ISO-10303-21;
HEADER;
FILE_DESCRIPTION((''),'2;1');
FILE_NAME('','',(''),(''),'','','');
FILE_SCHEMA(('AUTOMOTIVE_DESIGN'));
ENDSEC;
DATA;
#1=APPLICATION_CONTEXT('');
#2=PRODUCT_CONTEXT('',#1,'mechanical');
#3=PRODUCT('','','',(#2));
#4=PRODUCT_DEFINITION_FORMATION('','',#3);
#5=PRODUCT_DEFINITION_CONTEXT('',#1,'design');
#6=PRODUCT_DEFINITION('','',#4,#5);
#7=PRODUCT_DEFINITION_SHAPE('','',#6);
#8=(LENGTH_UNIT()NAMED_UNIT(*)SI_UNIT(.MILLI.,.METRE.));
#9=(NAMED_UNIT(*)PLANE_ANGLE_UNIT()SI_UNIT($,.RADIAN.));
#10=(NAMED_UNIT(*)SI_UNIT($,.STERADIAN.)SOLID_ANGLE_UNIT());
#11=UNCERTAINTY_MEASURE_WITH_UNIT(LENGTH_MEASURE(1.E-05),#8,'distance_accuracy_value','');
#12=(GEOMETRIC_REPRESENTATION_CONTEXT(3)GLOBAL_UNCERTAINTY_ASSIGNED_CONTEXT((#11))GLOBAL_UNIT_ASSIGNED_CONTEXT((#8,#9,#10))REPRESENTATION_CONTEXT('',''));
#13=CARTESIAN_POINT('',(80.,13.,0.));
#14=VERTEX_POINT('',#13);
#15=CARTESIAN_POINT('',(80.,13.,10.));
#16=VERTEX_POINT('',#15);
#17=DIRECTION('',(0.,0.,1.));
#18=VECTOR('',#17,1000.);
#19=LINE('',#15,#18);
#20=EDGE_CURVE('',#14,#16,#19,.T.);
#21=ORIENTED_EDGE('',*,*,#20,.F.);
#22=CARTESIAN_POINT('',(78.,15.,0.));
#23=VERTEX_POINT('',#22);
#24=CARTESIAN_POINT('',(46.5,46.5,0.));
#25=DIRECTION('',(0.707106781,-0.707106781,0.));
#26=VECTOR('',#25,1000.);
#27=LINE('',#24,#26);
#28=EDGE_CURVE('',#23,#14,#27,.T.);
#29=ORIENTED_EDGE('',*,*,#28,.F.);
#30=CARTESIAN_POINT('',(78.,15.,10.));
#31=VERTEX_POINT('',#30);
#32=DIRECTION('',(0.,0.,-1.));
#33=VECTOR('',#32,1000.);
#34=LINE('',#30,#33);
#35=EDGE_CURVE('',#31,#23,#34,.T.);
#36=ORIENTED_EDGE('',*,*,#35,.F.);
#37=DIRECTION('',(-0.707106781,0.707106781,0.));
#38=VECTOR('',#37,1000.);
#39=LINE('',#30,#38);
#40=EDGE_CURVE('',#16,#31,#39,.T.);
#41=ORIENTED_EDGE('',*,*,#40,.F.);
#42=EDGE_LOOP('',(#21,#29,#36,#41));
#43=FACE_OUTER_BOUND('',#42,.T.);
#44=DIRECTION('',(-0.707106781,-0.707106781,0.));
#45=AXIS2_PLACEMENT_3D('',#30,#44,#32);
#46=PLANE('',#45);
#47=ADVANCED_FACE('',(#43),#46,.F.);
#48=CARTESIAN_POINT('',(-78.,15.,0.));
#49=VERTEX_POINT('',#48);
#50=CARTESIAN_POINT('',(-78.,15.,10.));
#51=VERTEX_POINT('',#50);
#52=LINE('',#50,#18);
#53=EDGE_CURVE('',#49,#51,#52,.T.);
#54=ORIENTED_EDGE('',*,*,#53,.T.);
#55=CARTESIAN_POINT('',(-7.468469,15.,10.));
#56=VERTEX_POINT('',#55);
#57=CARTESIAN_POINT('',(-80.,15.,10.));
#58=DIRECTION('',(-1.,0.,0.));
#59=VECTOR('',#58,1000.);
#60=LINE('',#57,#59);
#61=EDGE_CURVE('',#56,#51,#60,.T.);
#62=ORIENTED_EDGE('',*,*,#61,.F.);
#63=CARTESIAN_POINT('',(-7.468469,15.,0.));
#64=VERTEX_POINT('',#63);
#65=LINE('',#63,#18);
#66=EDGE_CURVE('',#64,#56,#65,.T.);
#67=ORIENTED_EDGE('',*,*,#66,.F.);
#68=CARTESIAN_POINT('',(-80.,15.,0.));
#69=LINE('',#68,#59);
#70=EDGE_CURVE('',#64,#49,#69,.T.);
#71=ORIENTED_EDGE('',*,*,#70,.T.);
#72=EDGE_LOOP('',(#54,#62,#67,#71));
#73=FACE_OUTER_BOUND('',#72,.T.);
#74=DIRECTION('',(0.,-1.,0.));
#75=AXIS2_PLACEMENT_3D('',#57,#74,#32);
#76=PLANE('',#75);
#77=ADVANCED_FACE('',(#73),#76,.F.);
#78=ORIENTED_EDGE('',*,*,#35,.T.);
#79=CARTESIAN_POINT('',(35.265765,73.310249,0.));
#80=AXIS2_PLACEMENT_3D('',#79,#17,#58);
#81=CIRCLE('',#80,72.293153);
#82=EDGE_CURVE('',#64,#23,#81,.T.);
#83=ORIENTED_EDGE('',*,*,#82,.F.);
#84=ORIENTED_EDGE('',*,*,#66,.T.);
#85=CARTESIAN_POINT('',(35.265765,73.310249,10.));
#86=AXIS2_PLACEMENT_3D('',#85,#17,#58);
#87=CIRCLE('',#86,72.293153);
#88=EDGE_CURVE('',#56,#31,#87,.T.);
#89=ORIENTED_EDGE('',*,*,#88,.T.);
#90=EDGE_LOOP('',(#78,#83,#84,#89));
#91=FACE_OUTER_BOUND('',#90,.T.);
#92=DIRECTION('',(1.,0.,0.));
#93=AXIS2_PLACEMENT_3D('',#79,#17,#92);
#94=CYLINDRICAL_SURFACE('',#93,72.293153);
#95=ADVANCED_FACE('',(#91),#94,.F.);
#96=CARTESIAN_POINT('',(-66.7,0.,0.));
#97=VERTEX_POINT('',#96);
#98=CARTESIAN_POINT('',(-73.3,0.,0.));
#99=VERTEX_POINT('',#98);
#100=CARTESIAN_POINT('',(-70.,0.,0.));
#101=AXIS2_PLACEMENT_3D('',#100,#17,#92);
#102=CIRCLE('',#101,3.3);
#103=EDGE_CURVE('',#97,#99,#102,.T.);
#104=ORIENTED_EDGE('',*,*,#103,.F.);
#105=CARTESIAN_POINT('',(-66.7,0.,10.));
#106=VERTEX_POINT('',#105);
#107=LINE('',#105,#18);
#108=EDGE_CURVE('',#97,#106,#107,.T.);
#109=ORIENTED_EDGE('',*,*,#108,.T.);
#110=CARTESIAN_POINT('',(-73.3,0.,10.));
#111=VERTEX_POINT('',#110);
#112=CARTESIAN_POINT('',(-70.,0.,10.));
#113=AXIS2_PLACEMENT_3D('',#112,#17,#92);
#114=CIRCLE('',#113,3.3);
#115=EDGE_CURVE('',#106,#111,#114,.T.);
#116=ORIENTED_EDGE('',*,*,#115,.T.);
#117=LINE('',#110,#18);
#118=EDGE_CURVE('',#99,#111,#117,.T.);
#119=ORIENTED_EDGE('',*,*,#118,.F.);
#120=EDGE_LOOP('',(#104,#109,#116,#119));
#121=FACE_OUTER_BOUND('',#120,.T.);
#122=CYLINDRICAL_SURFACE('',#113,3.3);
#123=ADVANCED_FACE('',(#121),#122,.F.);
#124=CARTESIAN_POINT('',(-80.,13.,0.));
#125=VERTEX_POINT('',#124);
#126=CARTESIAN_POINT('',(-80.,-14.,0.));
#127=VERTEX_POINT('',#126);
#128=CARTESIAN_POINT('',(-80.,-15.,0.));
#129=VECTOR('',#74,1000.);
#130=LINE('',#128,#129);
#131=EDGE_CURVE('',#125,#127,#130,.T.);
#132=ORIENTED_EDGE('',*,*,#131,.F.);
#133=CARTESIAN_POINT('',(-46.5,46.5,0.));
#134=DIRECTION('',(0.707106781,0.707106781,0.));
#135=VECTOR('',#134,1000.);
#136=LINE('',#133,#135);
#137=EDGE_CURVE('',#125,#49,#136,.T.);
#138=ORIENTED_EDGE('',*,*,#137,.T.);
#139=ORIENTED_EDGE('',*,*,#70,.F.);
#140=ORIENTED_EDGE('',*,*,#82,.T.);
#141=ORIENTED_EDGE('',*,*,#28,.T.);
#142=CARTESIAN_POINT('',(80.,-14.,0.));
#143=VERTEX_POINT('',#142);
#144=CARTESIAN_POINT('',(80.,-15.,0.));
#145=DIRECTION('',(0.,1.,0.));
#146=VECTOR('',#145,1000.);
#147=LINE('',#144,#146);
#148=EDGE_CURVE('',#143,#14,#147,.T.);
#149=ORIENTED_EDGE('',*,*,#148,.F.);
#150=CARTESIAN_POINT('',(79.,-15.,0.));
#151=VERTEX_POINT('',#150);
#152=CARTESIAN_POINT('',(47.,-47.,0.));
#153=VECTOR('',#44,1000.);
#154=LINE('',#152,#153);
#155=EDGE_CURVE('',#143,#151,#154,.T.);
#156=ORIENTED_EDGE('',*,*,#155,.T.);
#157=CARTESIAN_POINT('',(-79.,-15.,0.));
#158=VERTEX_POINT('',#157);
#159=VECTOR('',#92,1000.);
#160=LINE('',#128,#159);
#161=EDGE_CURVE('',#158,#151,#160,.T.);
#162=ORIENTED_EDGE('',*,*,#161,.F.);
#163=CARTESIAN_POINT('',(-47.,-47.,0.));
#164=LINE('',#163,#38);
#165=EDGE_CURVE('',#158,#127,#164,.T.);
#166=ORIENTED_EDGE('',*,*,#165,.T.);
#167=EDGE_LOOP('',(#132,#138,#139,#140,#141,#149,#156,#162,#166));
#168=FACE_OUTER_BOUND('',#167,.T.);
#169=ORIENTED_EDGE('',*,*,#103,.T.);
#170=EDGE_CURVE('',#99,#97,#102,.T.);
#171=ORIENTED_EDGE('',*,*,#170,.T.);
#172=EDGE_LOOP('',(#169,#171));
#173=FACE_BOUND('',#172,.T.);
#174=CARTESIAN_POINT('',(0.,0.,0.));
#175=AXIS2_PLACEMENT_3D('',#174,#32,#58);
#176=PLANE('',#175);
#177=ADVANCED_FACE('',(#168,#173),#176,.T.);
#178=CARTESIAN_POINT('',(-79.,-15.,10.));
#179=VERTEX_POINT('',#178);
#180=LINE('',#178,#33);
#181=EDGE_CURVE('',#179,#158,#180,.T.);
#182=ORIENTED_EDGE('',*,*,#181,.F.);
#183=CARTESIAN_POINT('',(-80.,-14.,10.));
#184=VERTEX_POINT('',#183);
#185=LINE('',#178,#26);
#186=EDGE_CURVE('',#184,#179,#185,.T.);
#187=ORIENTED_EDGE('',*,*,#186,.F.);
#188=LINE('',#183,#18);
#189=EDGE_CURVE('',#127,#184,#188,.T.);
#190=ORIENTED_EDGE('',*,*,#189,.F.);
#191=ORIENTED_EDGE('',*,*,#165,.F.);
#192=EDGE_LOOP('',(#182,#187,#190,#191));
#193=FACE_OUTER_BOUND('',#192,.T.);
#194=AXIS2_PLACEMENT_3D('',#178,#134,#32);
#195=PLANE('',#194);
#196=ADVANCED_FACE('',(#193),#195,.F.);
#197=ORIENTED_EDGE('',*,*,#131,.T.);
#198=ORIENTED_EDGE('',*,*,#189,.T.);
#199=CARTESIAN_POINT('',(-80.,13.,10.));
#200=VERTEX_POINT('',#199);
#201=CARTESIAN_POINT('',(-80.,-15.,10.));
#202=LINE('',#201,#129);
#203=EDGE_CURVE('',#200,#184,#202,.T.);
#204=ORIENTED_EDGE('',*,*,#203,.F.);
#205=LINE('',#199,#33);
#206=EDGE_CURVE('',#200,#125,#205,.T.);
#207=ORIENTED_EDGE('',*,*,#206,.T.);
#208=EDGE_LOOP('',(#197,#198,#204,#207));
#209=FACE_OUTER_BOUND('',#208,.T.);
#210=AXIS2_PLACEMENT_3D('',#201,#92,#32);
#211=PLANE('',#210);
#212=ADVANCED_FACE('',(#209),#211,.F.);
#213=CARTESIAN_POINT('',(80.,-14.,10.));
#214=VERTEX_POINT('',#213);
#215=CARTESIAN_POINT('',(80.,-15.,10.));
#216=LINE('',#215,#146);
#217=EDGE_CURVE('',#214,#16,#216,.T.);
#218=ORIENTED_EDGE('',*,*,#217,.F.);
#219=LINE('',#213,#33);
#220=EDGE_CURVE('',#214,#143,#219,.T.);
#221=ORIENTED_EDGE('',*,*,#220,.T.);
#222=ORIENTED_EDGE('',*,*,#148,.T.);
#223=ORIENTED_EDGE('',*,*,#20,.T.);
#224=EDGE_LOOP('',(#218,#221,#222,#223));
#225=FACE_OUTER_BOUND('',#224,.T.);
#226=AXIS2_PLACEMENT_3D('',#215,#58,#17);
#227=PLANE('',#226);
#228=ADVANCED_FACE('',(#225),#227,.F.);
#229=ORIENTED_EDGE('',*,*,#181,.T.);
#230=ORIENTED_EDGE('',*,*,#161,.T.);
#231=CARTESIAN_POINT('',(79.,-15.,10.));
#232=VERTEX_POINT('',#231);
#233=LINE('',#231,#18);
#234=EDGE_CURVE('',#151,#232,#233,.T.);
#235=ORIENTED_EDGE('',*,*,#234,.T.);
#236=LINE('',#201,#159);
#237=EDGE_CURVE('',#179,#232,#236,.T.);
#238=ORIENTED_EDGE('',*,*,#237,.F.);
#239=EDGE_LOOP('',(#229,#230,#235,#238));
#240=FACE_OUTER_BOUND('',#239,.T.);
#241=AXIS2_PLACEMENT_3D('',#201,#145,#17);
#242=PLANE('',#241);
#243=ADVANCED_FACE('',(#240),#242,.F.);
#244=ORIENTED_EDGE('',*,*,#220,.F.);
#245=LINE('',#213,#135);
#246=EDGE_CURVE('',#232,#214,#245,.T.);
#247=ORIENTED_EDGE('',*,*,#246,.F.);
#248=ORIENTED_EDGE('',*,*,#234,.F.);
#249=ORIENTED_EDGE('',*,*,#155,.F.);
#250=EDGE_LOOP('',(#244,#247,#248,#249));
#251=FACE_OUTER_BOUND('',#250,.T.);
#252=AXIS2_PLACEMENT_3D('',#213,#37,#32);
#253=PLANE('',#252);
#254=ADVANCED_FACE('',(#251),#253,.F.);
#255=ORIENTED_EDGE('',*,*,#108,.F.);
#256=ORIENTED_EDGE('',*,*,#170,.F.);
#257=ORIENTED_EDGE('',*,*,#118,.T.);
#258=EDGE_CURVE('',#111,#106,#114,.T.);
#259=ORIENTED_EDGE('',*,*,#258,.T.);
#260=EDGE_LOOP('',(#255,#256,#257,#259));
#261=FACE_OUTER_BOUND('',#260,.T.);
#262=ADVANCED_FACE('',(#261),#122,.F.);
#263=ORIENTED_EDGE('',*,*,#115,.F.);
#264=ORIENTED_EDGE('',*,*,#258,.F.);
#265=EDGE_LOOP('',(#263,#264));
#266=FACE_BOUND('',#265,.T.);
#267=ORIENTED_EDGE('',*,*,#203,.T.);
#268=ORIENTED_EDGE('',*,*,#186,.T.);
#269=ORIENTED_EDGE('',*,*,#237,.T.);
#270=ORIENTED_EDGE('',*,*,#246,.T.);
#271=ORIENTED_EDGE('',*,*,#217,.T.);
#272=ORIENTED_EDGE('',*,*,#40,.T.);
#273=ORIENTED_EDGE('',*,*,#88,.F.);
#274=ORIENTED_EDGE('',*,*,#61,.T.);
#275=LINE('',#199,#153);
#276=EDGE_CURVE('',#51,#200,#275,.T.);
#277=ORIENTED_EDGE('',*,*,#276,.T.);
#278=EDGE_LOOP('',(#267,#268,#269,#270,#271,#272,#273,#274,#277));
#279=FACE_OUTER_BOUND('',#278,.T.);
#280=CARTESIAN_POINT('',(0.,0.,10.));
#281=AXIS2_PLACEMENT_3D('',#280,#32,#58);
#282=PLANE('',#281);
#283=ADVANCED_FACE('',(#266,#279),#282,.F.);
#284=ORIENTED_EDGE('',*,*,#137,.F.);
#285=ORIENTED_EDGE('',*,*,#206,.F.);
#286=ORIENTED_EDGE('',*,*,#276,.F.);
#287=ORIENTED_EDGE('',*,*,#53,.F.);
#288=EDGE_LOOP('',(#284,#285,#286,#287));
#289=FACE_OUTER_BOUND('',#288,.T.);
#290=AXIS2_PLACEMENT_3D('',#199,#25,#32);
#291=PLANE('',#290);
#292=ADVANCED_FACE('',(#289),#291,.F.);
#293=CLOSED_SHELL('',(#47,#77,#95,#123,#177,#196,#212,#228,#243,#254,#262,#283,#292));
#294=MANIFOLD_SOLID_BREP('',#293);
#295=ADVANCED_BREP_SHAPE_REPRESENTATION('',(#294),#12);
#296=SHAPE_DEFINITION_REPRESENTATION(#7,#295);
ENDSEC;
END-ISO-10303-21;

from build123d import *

# Parameters (mm, degrees)
SKETCH_1_W          = 160
SKETCH_1_H          = 30
EXTRUDE_1_DEPTH     = 10
CHAMFER_1_SIZE      = 2
CHAMFER_2_SIZE      = 1
HOLE_WIZARD_M6_1_D  = 6.6
CUT_EXTRUDE_1_DEPTH = 83.006097334


with BuildPart() as part:
    # 草图1 → 凸台-拉伸1 (new body)
    with BuildSketch(Plane.XY):
        Rectangle(SKETCH_1_W, SKETCH_1_H)
    extrude(amount=EXTRUDE_1_DEPTH)

    # 倒角1
    chamfer_1_edges = [part.edges().sort_by_distance(p)[0] for p in [
        (-80, 15, 5),
        (80, 15, 5),
    ]]
    chamfer(chamfer_1_edges, length=CHAMFER_1_SIZE)

    # 倒角2
    chamfer_2_edges = [part.edges().sort_by_distance(p)[0] for p in [
        (80, -15, 5),
        (-80, -15, 5),
    ]]
    chamfer(chamfer_2_edges, length=CHAMFER_2_SIZE)

    # M6 间隙孔1 (through all)
    with Locations(Plane.XY.offset(10)):
        with Locations((-70, 0)):
            Hole(HOLE_WIZARD_M6_1_D / 2)

    # 草图4 → 切除-拉伸1 (cut, through all)
    with BuildSketch(Plane.XY.offset(10)):
        with BuildLine():
            Line((-7.46846906, 15), (78, 15))
            ThreePointArc((78, 15), (35.26576547, 1.017096174), (-7.46846906, 15))
        make_face()
    extrude(amount=-CUT_EXTRUDE_1_DEPTH, mode=Mode.SUBTRACT)


solid = part.part
